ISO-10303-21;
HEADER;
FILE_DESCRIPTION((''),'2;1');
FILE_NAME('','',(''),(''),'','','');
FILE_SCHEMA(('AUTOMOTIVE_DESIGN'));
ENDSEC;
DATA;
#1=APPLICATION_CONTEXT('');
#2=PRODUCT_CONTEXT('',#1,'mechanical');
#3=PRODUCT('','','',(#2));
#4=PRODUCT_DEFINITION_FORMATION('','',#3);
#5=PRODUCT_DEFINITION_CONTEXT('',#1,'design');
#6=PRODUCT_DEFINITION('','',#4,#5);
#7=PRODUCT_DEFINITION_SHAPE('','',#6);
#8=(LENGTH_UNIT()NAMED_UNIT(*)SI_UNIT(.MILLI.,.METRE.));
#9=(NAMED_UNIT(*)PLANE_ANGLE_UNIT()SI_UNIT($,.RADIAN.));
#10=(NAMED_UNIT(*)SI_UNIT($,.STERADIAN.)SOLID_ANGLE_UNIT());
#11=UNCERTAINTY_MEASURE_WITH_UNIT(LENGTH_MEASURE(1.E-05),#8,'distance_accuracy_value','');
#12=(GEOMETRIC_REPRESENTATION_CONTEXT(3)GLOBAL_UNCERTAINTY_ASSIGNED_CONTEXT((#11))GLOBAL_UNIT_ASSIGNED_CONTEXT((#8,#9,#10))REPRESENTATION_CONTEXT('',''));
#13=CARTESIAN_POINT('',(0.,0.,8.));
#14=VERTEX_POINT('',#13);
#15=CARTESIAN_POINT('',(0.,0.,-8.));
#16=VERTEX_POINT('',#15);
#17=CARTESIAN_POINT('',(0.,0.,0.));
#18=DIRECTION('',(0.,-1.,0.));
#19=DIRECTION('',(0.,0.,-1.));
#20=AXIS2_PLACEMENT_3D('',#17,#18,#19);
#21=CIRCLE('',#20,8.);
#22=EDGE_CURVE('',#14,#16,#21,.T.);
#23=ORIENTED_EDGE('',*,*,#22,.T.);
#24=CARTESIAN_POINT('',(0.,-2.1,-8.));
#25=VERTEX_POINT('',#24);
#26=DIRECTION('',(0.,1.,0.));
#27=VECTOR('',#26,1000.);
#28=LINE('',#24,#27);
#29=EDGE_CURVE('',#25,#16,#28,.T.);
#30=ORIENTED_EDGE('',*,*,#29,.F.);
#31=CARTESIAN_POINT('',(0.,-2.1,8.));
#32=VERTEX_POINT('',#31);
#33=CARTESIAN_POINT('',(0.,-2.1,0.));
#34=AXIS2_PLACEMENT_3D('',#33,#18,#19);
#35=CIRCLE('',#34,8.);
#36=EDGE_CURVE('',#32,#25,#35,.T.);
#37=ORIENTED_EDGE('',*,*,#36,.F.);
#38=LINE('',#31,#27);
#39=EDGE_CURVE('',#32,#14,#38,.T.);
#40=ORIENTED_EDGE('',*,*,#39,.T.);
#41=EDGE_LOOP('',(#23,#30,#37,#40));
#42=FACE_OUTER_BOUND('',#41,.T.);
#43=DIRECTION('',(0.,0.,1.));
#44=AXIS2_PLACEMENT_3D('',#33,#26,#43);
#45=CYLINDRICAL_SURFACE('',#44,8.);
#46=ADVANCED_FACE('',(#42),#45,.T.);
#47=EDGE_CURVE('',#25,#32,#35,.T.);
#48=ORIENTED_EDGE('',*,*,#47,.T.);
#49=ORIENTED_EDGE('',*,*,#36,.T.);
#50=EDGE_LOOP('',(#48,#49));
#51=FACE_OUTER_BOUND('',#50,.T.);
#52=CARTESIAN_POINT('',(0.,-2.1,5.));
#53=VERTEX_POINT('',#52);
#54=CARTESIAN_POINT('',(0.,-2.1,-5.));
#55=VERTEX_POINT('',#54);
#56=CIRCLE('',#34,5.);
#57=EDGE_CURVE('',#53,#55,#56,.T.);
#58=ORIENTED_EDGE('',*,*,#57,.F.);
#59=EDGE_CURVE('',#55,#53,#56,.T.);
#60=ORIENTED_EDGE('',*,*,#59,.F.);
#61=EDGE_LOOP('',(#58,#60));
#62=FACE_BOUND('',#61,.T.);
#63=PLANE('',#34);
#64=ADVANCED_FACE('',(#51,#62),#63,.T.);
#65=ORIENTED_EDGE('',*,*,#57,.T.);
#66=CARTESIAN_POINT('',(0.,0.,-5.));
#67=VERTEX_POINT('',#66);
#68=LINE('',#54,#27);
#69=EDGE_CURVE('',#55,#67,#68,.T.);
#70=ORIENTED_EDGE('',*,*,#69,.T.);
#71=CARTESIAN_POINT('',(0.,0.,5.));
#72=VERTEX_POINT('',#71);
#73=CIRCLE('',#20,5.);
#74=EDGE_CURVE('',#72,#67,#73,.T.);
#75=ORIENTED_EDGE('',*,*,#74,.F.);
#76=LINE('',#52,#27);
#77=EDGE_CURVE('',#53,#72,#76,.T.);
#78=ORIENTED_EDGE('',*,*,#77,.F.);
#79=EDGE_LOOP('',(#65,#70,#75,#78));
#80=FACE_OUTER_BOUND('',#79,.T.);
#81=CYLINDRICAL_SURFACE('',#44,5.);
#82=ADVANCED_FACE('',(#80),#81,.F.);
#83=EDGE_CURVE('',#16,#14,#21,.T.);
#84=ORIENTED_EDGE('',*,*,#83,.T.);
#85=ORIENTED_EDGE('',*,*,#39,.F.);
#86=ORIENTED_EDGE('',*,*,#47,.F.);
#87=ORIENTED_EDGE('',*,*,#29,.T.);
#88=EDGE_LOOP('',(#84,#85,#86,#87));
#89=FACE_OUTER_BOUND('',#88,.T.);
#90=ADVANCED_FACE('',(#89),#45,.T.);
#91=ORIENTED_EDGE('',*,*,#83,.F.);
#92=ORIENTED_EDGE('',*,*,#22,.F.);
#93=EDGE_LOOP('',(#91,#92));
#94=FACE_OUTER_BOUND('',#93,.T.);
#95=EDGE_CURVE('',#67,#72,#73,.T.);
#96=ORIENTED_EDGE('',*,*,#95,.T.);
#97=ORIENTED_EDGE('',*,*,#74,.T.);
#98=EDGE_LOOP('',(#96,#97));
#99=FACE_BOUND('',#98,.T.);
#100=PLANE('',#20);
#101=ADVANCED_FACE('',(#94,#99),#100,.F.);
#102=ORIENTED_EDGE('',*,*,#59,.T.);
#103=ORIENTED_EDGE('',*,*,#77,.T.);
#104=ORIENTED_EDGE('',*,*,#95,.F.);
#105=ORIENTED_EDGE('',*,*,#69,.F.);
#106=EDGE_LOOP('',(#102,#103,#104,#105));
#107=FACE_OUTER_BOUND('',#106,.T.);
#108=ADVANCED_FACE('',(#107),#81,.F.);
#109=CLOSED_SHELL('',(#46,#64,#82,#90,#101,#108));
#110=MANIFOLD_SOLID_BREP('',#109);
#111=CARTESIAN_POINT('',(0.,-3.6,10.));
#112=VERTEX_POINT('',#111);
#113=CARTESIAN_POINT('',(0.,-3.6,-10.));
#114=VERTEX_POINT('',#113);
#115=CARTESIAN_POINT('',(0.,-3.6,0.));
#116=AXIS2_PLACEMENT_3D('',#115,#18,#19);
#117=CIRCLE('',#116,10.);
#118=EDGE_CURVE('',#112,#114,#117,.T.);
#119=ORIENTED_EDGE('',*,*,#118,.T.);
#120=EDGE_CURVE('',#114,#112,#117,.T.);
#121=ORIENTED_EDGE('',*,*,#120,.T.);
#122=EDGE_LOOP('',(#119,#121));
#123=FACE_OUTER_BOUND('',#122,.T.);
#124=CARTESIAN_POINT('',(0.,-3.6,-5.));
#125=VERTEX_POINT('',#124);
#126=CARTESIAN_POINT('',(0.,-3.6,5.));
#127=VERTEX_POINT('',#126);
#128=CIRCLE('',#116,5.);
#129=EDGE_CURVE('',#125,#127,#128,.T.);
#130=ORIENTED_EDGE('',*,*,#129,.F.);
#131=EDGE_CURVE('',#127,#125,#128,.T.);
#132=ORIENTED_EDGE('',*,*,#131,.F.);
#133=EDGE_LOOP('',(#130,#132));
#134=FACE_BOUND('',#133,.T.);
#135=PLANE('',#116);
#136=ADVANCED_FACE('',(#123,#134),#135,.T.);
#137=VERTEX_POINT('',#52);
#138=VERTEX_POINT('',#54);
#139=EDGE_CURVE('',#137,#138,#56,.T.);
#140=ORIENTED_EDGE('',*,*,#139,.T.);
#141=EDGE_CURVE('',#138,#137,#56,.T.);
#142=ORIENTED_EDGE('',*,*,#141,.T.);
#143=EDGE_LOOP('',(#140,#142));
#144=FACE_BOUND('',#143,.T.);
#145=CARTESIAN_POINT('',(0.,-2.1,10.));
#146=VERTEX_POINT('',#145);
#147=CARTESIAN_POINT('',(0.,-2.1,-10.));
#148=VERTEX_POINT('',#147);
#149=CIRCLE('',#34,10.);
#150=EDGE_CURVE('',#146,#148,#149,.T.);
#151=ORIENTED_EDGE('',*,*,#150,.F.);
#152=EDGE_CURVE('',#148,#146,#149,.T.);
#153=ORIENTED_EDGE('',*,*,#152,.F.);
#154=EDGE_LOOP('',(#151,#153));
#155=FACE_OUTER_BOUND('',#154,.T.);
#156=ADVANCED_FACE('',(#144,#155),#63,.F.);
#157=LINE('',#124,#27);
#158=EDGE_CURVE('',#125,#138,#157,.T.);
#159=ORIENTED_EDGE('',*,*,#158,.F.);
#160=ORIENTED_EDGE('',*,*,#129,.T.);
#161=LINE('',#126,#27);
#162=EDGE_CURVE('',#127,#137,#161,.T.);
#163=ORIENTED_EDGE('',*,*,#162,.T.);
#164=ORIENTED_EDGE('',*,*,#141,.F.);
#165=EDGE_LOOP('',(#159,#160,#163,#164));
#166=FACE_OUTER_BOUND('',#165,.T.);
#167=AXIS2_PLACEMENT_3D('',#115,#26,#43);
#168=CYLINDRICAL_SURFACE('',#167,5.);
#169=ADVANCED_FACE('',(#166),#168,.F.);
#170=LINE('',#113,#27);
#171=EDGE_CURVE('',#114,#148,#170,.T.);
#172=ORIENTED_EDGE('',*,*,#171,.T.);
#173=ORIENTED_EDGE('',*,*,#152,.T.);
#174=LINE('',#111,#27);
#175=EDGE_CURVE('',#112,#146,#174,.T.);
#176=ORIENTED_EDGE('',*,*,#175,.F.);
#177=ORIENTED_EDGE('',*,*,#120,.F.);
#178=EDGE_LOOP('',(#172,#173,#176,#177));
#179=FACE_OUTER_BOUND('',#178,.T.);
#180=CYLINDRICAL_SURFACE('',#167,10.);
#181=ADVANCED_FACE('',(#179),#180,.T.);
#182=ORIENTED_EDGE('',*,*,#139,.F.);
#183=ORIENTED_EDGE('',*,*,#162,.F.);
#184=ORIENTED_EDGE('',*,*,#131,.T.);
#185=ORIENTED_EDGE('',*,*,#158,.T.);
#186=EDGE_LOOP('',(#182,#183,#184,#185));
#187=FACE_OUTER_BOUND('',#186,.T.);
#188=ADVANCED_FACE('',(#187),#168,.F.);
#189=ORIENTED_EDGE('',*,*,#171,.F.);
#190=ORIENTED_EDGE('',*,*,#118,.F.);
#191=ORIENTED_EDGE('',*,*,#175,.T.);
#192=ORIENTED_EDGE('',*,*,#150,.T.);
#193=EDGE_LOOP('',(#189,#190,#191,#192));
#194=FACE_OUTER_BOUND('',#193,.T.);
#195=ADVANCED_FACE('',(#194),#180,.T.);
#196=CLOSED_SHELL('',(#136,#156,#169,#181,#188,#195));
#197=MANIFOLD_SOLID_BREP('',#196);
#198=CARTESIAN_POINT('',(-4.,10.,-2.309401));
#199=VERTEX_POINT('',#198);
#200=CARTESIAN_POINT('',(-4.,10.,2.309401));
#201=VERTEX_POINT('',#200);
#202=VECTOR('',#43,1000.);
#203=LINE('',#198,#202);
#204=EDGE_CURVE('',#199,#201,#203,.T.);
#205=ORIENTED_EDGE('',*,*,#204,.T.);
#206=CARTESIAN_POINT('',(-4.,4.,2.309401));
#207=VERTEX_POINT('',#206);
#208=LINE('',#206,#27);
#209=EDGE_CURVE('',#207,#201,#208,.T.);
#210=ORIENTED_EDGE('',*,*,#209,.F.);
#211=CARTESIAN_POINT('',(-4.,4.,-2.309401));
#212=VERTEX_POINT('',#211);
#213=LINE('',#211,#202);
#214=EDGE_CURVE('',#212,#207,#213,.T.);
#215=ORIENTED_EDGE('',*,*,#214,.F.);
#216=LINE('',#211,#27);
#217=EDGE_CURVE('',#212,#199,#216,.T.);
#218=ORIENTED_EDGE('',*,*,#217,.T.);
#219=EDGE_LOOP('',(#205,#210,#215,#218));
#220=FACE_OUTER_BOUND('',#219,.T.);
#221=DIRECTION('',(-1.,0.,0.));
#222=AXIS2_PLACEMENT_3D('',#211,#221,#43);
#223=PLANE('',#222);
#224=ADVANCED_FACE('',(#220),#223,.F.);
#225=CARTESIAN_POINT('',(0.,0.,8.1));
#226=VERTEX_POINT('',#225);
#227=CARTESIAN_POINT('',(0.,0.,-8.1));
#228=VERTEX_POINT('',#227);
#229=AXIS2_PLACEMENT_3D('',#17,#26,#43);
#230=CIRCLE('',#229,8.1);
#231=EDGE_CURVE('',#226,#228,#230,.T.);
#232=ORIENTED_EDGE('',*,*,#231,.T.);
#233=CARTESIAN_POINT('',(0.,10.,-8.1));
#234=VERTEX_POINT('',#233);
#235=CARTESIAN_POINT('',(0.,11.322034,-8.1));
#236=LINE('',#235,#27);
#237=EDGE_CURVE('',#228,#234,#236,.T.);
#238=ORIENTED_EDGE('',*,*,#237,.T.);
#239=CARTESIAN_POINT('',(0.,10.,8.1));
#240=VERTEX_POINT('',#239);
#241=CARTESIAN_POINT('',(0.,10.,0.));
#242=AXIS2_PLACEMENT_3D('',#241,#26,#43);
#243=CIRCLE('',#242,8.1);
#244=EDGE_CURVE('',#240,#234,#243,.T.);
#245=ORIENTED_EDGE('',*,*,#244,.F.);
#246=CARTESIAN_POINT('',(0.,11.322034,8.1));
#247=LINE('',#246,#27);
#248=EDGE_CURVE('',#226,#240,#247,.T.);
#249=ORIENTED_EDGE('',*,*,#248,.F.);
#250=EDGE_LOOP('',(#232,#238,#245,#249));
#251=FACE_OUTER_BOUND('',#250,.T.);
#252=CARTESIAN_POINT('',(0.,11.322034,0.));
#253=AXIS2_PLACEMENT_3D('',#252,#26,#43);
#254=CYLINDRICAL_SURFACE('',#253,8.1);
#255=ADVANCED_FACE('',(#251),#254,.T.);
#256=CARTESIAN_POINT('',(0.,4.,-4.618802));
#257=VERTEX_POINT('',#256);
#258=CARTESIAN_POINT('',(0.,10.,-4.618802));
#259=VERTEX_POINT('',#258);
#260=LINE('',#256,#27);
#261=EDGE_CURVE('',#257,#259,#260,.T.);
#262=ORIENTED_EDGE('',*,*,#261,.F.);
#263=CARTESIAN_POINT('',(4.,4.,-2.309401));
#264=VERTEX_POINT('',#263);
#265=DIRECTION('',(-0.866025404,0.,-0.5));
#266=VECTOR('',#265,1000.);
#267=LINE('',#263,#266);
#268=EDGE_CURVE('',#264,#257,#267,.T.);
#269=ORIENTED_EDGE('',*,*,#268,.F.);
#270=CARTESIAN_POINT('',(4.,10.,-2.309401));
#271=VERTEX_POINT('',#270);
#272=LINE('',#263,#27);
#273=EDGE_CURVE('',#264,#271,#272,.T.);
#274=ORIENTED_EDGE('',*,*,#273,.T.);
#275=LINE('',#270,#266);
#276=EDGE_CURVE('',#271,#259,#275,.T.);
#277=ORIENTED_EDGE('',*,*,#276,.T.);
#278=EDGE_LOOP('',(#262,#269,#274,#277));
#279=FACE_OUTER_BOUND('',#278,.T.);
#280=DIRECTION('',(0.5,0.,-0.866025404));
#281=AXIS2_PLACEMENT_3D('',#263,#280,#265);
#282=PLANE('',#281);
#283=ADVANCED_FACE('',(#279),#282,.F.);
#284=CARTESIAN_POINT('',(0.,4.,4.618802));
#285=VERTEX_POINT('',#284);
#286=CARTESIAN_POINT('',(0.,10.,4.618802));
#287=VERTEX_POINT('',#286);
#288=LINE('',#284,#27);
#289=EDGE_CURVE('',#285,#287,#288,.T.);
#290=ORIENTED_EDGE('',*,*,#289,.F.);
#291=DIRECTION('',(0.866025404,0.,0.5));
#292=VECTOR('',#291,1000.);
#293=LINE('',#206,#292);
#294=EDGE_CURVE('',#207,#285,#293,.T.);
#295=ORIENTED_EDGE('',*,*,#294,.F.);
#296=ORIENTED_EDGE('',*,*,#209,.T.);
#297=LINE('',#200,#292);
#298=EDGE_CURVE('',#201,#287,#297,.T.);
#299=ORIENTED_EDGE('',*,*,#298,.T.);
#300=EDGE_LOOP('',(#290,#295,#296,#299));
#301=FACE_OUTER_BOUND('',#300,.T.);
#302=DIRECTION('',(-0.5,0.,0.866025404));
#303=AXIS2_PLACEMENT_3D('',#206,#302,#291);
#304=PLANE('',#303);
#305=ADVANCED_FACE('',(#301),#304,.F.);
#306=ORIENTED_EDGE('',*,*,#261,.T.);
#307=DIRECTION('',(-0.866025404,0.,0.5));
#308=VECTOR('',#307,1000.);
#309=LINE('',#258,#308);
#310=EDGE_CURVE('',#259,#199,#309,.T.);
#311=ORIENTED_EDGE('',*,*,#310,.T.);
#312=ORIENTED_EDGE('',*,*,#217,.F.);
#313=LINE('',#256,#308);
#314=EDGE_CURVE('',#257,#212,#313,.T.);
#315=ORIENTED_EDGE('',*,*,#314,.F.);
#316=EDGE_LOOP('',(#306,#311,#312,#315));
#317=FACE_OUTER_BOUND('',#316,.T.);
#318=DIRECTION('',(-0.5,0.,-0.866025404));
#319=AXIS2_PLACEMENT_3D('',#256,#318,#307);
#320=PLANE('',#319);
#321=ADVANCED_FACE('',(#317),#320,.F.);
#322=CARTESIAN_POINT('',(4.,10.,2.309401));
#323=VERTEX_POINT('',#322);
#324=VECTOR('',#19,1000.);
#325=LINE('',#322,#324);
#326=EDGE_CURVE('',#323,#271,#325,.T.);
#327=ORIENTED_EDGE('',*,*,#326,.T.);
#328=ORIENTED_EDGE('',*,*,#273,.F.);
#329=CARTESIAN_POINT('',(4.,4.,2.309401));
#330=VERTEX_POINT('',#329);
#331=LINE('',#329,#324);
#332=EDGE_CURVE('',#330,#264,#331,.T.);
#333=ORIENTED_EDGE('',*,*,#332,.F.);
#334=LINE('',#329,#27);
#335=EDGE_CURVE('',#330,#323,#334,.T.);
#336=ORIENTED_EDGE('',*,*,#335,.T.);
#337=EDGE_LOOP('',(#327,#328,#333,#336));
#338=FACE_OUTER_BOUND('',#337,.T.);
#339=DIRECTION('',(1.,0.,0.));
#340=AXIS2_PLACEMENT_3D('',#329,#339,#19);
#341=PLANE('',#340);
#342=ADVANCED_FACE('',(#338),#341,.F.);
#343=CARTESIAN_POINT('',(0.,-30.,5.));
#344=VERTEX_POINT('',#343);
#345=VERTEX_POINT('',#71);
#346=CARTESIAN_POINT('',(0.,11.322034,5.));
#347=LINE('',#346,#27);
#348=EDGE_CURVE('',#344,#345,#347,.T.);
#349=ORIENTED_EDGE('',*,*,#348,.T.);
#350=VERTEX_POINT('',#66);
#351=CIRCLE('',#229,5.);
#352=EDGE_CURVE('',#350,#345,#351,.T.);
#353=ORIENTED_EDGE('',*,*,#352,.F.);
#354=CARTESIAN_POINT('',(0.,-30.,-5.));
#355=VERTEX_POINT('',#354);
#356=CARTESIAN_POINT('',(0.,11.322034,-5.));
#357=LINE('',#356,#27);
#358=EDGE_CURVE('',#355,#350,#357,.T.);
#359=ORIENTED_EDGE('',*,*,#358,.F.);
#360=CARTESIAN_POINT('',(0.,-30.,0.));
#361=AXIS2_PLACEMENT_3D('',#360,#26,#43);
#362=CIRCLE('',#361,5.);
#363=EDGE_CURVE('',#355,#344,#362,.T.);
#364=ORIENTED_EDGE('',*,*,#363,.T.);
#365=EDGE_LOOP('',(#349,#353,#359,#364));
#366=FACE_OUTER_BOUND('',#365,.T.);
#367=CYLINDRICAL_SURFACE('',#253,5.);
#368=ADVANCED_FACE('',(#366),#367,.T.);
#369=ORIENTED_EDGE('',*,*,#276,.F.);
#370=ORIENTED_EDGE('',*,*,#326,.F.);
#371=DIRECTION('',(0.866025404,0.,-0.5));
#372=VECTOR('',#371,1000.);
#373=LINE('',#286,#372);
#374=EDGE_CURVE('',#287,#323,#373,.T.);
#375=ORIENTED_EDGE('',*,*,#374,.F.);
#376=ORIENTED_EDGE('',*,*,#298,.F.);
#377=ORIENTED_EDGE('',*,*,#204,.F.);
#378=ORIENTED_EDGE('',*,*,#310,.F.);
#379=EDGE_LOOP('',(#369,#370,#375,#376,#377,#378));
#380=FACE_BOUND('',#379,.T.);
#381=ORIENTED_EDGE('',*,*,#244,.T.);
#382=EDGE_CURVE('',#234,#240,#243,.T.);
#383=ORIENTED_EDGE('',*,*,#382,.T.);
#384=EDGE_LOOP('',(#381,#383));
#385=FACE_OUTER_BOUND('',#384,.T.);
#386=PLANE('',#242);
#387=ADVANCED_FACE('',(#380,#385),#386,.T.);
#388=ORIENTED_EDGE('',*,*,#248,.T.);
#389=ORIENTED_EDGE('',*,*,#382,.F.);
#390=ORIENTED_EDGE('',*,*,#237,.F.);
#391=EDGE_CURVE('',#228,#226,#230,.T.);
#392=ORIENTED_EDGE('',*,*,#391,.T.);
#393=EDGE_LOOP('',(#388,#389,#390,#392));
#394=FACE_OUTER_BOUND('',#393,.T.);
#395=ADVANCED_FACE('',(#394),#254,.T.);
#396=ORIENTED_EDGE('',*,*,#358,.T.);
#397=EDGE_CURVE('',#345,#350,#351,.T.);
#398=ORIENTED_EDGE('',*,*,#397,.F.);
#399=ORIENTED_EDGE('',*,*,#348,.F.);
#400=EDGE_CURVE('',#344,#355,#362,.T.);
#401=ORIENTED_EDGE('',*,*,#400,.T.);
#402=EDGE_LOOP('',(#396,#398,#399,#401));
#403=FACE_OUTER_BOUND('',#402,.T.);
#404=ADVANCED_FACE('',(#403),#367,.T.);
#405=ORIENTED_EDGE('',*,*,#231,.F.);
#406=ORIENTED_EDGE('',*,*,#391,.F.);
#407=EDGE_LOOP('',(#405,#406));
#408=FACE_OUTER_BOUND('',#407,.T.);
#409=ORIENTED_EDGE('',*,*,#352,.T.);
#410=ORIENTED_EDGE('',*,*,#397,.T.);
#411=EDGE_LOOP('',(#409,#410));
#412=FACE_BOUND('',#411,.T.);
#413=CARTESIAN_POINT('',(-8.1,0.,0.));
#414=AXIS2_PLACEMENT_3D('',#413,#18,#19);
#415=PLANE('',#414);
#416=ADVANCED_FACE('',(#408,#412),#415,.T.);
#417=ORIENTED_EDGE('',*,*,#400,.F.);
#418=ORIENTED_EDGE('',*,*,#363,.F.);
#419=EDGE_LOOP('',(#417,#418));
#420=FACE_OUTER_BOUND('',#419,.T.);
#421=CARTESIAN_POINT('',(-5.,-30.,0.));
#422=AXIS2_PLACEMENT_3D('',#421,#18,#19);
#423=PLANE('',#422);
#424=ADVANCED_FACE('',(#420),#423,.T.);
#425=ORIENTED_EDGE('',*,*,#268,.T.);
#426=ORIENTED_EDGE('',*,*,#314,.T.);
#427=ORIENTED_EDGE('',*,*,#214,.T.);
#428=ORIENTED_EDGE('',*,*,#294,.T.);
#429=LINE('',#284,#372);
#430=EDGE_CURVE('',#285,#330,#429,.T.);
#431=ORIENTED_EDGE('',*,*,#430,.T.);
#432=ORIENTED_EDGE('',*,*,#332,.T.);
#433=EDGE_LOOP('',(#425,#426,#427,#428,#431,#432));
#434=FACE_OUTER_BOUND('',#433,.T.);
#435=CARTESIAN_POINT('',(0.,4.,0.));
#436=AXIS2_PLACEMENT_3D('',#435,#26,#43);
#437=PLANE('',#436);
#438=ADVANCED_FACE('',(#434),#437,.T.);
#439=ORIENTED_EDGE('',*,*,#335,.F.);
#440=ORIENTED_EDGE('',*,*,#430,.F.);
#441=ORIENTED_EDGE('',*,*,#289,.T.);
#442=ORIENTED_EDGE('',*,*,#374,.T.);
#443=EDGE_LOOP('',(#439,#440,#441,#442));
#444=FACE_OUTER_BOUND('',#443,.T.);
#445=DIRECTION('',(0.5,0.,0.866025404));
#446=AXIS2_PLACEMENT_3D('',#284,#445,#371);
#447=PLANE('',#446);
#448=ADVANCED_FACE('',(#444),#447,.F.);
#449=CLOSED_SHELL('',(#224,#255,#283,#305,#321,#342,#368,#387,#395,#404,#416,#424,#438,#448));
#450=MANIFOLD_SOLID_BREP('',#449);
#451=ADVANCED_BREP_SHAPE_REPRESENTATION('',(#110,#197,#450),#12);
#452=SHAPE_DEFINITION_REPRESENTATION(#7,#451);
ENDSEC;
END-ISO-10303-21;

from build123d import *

# Parameters (mm, degrees)
CUT_EXTRUDE_1_DEPTH  = 6
SKETCH_3_R           = 8
SKETCH_3_R_2         = 5
BOSS_EXTRUDE_1_DEPTH = 2.1
SKETCH_4_R           = 10
SKETCH_4_R_2         = 5
BOSS_EXTRUDE_2_DEPTH = 1.5


with BuildPart() as part:
    # Sketch 1 → Revolve 1 (revolve)
    with BuildSketch(Plane.XY, mode=Mode.PRIVATE) as revolve_1_sk:
        Polygon((0, 10), (-8.1, 10), (-8.1, 0), (-5, 0), (-5, -30), (0, -30), align=None)
    revolve(revolve_1_sk.sketch.rotate(Axis((0, 11.322033898, 0), (0, -1, 0)), 270), axis=Axis((0, 11.322033898, 0), (0, -1, 0)))

    # Sketch 2 → Cut-Extrude 1 (cut)
    with BuildSketch(Plane(origin=(0, 10, 0), x_dir=(1, 0, 0), z_dir=(0, 1, 0))):
        Polygon((0, 4.618802154), (-4, 2.309401077), (-4, -2.309401077), (0, -4.618802154), (4, -2.309401077), (4, 2.309401077), align=None)
    extrude(amount=-CUT_EXTRUDE_1_DEPTH, mode=Mode.SUBTRACT)


with BuildPart() as body_2:
    # Sketch 3 → Boss-Extrude 1 (new body)
    with BuildSketch(Plane.XZ):
        with Locations(Location((0, 0, 0), (0, 0, 270))):
            Circle(SKETCH_3_R)
        with Locations(Location((0, 0, 0), (0, 0, 270))):
            Circle(SKETCH_3_R_2, mode=Mode.SUBTRACT)
    extrude(amount=BOSS_EXTRUDE_1_DEPTH)


with BuildPart() as body_3:
    # Sketch 4 → Boss-Extrude 2 (new body)
    with BuildSketch(Plane.XZ.offset(2.1)):
        with Locations(Location((0, 0, 0), (0, 0, 270))):
            Circle(SKETCH_4_R)
        with Locations(Location((0, 0, 0), (0, 0, 270))):
            Circle(SKETCH_4_R_2, mode=Mode.SUBTRACT)
    extrude(amount=BOSS_EXTRUDE_2_DEPTH)


solid = Compound([part.part, body_2.part, body_3.part])
